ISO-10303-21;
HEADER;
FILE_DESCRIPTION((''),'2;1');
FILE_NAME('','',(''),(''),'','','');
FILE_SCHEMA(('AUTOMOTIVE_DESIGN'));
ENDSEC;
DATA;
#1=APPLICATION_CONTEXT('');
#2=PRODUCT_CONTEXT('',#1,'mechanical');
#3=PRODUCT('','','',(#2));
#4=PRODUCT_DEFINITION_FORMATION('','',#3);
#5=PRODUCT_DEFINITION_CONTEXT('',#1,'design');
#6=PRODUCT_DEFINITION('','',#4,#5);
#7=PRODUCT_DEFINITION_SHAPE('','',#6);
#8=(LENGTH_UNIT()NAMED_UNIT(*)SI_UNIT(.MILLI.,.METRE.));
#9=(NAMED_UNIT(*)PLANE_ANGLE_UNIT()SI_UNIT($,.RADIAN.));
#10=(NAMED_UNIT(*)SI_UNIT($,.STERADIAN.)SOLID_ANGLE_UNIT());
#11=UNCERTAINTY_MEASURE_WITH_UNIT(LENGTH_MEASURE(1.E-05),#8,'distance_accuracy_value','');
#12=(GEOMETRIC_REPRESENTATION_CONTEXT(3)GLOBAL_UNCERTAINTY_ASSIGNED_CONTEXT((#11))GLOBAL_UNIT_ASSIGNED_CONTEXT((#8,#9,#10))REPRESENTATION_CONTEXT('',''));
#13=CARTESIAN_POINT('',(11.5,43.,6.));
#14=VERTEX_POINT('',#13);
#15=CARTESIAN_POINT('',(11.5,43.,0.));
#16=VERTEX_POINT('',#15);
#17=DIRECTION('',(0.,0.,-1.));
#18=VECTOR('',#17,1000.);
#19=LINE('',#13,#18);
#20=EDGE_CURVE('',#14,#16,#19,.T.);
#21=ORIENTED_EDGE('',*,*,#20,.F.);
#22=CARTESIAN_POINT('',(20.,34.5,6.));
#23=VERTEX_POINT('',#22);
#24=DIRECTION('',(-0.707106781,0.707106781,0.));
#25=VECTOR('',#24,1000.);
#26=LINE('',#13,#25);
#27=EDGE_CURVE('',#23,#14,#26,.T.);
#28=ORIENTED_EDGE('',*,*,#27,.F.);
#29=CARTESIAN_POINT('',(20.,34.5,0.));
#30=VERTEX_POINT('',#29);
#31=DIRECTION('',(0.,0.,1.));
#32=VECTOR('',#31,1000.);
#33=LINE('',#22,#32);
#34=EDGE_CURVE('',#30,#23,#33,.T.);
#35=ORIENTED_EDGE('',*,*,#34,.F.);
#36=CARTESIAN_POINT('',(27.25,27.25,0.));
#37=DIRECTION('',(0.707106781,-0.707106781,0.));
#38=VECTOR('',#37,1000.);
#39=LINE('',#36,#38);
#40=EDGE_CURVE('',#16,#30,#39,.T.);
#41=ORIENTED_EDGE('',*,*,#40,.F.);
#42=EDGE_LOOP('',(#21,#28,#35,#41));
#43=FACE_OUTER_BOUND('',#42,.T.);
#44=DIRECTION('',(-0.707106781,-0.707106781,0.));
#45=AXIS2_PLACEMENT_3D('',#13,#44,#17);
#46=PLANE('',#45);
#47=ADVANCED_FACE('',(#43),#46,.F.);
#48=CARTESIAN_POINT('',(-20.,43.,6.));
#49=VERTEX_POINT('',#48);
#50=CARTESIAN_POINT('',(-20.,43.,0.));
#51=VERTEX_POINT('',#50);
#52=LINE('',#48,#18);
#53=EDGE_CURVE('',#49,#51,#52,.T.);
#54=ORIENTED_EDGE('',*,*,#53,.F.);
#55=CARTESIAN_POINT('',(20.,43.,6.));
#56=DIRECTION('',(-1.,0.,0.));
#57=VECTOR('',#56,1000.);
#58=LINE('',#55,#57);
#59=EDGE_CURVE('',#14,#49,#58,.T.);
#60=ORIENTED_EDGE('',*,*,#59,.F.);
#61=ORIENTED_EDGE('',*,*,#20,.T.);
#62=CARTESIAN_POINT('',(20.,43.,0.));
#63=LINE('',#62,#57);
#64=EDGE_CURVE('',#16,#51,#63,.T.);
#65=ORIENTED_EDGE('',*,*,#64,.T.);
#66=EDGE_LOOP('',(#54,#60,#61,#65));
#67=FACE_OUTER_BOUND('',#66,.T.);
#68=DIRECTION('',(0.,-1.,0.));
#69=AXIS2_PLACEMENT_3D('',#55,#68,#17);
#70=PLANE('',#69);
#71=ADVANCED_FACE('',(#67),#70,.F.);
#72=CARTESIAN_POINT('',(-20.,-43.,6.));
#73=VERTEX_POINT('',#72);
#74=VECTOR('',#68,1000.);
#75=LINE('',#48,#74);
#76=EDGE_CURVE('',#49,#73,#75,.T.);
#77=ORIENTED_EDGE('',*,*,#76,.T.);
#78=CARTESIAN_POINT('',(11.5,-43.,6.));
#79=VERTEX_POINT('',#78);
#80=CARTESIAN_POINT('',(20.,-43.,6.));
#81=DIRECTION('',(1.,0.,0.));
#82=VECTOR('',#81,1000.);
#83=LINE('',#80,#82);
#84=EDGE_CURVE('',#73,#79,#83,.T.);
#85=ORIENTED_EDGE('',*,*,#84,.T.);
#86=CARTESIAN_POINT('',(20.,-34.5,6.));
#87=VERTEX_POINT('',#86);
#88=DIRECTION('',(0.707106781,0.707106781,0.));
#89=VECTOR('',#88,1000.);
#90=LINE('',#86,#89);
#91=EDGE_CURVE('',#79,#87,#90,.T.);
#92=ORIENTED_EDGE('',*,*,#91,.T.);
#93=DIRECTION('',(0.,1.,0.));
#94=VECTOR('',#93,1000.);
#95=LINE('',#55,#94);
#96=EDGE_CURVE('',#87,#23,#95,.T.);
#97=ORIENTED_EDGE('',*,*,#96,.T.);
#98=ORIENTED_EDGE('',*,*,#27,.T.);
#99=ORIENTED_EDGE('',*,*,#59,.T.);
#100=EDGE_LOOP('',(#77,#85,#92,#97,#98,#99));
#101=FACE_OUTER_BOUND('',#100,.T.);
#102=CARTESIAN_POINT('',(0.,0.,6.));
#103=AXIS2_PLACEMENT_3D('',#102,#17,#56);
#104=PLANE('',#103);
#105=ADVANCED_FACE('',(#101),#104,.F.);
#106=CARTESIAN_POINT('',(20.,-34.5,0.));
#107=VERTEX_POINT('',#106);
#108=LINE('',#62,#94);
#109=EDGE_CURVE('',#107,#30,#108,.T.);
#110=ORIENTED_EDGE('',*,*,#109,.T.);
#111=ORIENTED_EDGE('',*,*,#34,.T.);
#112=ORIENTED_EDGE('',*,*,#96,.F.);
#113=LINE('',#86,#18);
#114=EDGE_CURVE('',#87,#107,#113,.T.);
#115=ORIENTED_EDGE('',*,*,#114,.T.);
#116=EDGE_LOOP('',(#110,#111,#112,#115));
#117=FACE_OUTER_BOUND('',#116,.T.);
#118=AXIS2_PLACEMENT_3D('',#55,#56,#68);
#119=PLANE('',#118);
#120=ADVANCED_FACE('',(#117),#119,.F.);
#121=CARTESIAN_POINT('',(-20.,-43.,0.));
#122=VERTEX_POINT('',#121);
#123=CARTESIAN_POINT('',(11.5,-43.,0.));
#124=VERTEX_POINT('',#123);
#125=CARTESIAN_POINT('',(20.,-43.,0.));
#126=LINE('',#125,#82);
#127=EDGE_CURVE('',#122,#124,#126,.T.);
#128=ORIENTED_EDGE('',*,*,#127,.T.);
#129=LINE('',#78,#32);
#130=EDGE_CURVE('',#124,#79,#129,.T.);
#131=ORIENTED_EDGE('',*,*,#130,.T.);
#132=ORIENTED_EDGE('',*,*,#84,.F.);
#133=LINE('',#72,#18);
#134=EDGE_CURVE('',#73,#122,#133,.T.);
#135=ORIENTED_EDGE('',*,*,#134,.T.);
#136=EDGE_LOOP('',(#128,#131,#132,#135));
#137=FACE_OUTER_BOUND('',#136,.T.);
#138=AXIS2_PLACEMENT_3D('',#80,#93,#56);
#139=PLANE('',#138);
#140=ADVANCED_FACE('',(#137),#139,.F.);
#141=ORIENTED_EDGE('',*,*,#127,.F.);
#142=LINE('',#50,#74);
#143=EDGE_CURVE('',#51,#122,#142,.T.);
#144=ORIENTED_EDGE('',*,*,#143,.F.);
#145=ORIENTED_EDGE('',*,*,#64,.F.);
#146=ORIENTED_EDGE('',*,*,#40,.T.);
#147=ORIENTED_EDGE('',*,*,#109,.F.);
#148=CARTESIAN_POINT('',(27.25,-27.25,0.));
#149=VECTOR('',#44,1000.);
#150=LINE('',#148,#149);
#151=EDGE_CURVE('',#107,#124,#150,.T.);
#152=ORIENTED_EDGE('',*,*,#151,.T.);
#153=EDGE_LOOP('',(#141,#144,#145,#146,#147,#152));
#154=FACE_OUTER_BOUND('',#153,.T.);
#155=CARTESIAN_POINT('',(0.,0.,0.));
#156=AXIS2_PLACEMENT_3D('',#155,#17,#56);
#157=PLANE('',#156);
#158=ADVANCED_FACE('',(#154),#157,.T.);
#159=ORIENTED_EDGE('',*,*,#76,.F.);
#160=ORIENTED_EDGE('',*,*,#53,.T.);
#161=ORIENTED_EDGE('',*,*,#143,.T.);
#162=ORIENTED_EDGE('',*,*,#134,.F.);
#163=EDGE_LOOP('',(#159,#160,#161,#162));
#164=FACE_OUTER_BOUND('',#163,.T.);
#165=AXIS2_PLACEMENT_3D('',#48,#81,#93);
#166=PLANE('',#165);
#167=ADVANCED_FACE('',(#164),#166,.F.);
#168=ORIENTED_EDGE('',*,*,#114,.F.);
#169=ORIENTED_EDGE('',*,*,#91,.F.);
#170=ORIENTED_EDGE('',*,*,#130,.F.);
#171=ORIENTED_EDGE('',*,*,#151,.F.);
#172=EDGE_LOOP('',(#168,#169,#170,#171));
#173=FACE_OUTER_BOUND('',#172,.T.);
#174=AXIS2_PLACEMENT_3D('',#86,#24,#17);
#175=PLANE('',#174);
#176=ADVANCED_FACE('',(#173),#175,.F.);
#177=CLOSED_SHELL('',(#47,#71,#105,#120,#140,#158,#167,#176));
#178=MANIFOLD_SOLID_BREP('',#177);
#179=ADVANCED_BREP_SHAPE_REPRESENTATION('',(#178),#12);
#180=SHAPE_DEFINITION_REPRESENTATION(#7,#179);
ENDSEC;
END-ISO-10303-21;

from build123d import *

# Parameters (mm, degrees)
SKETCH1_W           = 40
SKETCH1_H           = 86
BOSS_EXTRUDE1_DEPTH = 6
CHAMFER1_SIZE       = 8.5


with BuildPart() as part:
    # Sketch1 → Boss-Extrude1 (new body)
    with BuildSketch(Plane.XY):
        Rectangle(SKETCH1_W, SKETCH1_H)
    extrude(amount=BOSS_EXTRUDE1_DEPTH)

    # Chamfer1
    chamfer1_edges = [part.edges().sort_by_distance(p)[0] for p in [
        (20, 43, 3),
        (20, -43, 3),
    ]]
    chamfer(chamfer1_edges, length=CHAMFER1_SIZE)


solid = part.part
